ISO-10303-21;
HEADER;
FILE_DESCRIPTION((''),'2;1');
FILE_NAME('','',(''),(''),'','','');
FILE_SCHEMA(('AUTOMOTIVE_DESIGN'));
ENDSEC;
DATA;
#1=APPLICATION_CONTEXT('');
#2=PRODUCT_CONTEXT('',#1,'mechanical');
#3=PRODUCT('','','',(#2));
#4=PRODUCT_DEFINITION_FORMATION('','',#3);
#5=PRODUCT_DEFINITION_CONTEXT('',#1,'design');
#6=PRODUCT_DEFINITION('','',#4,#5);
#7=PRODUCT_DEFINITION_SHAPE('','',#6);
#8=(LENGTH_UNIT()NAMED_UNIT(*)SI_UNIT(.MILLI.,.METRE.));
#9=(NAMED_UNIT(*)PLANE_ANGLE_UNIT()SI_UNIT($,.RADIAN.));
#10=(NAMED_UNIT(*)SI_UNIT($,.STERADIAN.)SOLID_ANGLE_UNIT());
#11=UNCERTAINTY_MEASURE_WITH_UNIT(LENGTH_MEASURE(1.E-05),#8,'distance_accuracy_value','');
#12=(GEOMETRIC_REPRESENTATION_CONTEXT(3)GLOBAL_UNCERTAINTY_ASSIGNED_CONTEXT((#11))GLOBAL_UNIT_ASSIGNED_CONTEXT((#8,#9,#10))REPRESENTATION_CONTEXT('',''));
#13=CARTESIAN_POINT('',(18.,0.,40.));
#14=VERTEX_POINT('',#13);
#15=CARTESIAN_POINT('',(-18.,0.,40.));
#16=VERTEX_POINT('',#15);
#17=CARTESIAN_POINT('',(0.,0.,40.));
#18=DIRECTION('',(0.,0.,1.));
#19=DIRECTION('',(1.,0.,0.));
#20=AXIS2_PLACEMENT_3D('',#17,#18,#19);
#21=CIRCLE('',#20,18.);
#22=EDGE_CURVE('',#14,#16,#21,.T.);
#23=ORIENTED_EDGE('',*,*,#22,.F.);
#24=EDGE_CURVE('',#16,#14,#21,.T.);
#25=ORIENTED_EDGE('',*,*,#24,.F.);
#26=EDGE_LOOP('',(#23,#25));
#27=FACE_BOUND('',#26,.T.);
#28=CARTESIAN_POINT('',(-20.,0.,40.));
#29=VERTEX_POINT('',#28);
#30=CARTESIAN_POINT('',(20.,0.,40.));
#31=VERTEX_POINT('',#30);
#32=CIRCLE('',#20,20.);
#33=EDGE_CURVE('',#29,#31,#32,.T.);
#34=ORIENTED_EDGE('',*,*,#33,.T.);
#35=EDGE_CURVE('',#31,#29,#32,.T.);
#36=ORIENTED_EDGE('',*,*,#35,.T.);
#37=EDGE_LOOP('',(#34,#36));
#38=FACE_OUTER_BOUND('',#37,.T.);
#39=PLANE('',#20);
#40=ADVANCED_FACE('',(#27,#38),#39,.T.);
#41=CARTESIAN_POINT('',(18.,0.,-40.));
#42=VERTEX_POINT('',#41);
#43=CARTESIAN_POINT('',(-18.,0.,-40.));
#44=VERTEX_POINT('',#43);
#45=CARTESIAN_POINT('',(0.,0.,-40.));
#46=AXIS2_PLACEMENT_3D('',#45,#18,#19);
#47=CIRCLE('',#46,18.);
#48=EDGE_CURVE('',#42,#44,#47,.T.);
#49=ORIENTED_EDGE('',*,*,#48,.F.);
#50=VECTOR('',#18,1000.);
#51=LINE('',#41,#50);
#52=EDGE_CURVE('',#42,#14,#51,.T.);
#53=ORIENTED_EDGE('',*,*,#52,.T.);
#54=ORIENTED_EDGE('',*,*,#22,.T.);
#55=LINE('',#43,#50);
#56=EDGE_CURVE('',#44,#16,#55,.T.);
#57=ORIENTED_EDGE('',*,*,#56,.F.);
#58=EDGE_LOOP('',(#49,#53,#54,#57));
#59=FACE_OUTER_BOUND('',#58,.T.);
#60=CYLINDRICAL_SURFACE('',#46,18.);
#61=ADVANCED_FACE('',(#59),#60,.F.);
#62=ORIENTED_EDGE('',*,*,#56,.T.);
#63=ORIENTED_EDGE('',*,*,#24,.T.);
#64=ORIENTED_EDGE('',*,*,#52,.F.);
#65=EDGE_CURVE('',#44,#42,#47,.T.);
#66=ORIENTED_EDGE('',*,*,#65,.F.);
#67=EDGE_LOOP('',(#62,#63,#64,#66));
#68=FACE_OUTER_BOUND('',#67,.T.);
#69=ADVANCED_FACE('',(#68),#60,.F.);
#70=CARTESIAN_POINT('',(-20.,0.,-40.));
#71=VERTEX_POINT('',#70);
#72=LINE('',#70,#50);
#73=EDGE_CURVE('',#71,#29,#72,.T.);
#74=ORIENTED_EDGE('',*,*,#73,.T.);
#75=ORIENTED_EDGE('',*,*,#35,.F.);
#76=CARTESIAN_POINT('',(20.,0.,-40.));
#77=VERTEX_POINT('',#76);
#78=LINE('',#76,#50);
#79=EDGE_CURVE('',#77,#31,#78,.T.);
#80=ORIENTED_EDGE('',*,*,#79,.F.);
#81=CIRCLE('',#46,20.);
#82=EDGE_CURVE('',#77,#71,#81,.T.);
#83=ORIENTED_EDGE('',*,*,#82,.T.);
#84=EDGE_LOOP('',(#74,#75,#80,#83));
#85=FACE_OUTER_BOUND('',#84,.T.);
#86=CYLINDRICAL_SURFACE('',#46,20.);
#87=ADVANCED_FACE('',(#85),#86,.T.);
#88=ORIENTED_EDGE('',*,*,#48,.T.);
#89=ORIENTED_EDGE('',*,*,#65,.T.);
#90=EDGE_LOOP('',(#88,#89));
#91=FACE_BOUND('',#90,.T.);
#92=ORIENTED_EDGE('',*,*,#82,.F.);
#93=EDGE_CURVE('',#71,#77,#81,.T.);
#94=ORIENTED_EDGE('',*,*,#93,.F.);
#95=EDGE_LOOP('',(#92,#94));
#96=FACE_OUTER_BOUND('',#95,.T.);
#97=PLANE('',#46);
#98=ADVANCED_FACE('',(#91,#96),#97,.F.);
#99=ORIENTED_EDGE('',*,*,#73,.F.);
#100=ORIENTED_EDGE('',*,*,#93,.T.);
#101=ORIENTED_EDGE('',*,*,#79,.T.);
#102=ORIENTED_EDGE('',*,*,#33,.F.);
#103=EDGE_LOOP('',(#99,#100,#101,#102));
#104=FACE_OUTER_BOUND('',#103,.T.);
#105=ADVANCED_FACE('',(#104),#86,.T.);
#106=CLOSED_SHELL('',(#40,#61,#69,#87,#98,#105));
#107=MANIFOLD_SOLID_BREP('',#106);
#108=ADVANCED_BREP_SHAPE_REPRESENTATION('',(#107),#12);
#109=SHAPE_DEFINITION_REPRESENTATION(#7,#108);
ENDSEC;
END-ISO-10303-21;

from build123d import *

# Parameters (mm, degrees)
SKETCH_1_R      = 20
SKETCH_1_R_2    = 18
EXTRUDE_1_DEPTH = 40


with BuildPart() as part:
    # 草图1 → 凸台-拉伸1 (new, symmetric)
    with BuildSketch(Plane.XY):
        Circle(SKETCH_1_R)
        Circle(SKETCH_1_R_2, mode=Mode.SUBTRACT)
    extrude(amount=EXTRUDE_1_DEPTH, both=True)


solid = part.part
